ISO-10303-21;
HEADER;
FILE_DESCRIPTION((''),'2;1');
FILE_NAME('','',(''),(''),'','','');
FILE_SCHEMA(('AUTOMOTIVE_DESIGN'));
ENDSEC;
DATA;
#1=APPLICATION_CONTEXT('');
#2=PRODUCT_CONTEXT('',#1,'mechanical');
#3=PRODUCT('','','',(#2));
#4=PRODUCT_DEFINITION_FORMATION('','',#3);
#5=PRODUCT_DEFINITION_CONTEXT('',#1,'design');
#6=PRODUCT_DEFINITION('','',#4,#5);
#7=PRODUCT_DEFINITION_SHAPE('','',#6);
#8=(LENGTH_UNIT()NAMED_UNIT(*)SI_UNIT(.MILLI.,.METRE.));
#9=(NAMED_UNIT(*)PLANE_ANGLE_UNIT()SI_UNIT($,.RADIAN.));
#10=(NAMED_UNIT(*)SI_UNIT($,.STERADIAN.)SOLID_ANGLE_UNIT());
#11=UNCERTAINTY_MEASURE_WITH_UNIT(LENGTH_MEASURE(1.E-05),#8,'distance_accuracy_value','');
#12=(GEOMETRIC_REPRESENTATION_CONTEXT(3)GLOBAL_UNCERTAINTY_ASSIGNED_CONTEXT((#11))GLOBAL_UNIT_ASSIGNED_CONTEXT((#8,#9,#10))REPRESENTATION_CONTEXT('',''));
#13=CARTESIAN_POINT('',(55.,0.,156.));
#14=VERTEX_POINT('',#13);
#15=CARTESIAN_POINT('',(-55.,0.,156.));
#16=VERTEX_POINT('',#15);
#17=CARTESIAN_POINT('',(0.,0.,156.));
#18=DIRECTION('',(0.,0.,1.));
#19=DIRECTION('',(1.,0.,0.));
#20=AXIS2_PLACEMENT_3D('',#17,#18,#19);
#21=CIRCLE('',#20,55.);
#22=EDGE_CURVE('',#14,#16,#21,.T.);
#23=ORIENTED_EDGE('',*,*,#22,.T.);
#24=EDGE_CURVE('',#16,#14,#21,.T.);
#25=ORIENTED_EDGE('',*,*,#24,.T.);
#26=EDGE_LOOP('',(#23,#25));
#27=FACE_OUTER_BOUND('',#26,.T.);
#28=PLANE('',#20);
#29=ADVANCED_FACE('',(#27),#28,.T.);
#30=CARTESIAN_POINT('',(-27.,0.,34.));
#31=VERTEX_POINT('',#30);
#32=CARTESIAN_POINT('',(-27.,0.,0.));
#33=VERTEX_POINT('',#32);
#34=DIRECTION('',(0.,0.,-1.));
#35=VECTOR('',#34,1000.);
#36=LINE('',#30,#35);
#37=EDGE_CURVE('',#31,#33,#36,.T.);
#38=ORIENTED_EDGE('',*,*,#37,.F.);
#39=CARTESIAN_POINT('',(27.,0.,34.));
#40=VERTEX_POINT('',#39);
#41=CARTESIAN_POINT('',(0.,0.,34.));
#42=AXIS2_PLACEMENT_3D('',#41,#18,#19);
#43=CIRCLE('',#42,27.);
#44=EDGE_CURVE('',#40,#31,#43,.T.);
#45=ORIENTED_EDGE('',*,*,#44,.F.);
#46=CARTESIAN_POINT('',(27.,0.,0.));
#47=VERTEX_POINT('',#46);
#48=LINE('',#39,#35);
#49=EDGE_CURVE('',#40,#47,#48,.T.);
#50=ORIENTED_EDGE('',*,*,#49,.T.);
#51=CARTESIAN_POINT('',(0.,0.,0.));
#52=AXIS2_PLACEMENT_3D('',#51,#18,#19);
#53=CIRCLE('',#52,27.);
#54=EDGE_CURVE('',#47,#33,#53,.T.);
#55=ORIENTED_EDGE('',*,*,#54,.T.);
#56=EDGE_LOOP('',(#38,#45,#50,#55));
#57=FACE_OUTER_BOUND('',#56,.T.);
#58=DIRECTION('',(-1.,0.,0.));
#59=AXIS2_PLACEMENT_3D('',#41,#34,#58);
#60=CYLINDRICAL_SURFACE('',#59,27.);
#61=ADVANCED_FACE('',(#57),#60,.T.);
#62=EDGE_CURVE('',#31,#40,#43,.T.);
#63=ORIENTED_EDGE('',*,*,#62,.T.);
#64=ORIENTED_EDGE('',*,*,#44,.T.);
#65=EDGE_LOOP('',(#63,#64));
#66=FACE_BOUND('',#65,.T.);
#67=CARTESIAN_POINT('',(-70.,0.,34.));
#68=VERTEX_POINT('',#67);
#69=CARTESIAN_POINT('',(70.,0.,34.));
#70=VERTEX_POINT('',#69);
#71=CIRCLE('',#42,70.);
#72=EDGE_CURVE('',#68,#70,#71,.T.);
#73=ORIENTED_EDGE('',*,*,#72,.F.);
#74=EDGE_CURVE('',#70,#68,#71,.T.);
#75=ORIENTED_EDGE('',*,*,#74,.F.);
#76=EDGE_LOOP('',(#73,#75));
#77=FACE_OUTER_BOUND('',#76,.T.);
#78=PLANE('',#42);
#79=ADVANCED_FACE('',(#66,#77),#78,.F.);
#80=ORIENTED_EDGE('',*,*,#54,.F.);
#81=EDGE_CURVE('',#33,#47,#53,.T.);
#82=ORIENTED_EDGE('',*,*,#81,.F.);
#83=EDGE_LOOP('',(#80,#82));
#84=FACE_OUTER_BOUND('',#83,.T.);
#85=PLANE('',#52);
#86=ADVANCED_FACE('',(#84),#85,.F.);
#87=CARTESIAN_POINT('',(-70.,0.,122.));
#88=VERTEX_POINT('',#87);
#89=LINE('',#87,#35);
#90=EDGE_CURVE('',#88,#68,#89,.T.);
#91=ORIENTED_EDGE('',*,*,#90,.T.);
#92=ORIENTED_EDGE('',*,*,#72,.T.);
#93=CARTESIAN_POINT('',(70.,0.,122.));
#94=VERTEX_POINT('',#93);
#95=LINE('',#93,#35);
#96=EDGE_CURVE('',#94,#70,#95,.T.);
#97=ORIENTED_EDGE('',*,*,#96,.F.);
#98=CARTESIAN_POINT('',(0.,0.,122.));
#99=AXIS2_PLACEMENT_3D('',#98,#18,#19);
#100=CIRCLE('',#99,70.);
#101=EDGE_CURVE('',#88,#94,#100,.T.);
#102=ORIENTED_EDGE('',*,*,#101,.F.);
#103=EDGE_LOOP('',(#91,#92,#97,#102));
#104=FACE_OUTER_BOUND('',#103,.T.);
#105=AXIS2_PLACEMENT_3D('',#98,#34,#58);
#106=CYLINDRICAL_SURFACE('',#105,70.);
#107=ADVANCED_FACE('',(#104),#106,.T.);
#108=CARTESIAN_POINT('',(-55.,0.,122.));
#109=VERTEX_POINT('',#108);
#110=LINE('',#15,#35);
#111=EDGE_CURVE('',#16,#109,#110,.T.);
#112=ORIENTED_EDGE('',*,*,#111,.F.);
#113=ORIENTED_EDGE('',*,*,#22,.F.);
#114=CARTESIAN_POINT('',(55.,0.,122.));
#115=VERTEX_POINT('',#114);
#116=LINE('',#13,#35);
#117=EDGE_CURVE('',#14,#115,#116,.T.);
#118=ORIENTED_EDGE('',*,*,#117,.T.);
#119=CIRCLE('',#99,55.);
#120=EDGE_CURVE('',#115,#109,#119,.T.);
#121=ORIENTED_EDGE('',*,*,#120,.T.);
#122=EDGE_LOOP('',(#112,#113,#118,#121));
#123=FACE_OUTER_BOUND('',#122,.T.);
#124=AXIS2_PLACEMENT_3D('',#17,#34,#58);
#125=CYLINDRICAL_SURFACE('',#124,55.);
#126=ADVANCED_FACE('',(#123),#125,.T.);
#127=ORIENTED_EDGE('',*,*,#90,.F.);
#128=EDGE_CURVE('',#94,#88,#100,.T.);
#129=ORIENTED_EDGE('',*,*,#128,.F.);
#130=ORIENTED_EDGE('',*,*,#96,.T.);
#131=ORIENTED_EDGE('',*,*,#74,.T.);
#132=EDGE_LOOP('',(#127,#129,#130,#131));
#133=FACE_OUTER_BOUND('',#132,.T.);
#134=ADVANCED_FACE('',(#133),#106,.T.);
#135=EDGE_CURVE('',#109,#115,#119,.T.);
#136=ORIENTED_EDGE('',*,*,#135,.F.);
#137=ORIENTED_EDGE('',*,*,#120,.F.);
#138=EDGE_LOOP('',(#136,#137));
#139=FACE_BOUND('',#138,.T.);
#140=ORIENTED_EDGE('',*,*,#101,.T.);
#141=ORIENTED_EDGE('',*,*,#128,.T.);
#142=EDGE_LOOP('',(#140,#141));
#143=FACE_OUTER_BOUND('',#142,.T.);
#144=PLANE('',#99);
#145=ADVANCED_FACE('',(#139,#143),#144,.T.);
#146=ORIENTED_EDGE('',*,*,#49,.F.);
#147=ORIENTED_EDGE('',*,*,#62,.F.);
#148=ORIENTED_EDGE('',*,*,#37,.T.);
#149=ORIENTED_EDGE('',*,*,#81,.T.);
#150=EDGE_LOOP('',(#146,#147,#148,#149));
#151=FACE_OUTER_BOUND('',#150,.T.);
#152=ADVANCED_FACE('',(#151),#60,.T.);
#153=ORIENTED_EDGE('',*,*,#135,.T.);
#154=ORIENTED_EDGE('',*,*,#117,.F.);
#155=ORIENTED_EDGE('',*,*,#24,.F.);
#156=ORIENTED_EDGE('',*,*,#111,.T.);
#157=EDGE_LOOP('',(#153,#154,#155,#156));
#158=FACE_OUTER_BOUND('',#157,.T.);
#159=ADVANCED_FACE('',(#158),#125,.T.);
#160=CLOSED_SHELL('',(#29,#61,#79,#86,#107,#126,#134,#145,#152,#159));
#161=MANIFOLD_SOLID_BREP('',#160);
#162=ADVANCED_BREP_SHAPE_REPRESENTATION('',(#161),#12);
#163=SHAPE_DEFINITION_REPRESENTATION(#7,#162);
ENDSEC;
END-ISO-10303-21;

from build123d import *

# Parameters (mm, degrees)
SKETCH1_R           = 27
BOSS_EXTRUDE1_DEPTH = 34
SKETCH2_R           = 70
BOSS_EXTRUDE2_DEPTH = 88
SKETCH3_R           = 55
BOSS_EXTRUDE3_DEPTH = 34


with BuildPart() as part:
    # Sketch1 → Boss-Extrude1 (new body)
    with BuildSketch(Plane.XY):
        Circle(SKETCH1_R)
    extrude(amount=BOSS_EXTRUDE1_DEPTH)

    # Sketch2 → Boss-Extrude2 (add)
    with BuildSketch(Plane.XY.offset(34)):
        Circle(SKETCH2_R)
    extrude(amount=BOSS_EXTRUDE2_DEPTH)

    # Sketch3 → Boss-Extrude3 (add)
    with BuildSketch(Plane.XY.offset(122)):
        Circle(SKETCH3_R)
    extrude(amount=BOSS_EXTRUDE3_DEPTH)


solid = part.part
